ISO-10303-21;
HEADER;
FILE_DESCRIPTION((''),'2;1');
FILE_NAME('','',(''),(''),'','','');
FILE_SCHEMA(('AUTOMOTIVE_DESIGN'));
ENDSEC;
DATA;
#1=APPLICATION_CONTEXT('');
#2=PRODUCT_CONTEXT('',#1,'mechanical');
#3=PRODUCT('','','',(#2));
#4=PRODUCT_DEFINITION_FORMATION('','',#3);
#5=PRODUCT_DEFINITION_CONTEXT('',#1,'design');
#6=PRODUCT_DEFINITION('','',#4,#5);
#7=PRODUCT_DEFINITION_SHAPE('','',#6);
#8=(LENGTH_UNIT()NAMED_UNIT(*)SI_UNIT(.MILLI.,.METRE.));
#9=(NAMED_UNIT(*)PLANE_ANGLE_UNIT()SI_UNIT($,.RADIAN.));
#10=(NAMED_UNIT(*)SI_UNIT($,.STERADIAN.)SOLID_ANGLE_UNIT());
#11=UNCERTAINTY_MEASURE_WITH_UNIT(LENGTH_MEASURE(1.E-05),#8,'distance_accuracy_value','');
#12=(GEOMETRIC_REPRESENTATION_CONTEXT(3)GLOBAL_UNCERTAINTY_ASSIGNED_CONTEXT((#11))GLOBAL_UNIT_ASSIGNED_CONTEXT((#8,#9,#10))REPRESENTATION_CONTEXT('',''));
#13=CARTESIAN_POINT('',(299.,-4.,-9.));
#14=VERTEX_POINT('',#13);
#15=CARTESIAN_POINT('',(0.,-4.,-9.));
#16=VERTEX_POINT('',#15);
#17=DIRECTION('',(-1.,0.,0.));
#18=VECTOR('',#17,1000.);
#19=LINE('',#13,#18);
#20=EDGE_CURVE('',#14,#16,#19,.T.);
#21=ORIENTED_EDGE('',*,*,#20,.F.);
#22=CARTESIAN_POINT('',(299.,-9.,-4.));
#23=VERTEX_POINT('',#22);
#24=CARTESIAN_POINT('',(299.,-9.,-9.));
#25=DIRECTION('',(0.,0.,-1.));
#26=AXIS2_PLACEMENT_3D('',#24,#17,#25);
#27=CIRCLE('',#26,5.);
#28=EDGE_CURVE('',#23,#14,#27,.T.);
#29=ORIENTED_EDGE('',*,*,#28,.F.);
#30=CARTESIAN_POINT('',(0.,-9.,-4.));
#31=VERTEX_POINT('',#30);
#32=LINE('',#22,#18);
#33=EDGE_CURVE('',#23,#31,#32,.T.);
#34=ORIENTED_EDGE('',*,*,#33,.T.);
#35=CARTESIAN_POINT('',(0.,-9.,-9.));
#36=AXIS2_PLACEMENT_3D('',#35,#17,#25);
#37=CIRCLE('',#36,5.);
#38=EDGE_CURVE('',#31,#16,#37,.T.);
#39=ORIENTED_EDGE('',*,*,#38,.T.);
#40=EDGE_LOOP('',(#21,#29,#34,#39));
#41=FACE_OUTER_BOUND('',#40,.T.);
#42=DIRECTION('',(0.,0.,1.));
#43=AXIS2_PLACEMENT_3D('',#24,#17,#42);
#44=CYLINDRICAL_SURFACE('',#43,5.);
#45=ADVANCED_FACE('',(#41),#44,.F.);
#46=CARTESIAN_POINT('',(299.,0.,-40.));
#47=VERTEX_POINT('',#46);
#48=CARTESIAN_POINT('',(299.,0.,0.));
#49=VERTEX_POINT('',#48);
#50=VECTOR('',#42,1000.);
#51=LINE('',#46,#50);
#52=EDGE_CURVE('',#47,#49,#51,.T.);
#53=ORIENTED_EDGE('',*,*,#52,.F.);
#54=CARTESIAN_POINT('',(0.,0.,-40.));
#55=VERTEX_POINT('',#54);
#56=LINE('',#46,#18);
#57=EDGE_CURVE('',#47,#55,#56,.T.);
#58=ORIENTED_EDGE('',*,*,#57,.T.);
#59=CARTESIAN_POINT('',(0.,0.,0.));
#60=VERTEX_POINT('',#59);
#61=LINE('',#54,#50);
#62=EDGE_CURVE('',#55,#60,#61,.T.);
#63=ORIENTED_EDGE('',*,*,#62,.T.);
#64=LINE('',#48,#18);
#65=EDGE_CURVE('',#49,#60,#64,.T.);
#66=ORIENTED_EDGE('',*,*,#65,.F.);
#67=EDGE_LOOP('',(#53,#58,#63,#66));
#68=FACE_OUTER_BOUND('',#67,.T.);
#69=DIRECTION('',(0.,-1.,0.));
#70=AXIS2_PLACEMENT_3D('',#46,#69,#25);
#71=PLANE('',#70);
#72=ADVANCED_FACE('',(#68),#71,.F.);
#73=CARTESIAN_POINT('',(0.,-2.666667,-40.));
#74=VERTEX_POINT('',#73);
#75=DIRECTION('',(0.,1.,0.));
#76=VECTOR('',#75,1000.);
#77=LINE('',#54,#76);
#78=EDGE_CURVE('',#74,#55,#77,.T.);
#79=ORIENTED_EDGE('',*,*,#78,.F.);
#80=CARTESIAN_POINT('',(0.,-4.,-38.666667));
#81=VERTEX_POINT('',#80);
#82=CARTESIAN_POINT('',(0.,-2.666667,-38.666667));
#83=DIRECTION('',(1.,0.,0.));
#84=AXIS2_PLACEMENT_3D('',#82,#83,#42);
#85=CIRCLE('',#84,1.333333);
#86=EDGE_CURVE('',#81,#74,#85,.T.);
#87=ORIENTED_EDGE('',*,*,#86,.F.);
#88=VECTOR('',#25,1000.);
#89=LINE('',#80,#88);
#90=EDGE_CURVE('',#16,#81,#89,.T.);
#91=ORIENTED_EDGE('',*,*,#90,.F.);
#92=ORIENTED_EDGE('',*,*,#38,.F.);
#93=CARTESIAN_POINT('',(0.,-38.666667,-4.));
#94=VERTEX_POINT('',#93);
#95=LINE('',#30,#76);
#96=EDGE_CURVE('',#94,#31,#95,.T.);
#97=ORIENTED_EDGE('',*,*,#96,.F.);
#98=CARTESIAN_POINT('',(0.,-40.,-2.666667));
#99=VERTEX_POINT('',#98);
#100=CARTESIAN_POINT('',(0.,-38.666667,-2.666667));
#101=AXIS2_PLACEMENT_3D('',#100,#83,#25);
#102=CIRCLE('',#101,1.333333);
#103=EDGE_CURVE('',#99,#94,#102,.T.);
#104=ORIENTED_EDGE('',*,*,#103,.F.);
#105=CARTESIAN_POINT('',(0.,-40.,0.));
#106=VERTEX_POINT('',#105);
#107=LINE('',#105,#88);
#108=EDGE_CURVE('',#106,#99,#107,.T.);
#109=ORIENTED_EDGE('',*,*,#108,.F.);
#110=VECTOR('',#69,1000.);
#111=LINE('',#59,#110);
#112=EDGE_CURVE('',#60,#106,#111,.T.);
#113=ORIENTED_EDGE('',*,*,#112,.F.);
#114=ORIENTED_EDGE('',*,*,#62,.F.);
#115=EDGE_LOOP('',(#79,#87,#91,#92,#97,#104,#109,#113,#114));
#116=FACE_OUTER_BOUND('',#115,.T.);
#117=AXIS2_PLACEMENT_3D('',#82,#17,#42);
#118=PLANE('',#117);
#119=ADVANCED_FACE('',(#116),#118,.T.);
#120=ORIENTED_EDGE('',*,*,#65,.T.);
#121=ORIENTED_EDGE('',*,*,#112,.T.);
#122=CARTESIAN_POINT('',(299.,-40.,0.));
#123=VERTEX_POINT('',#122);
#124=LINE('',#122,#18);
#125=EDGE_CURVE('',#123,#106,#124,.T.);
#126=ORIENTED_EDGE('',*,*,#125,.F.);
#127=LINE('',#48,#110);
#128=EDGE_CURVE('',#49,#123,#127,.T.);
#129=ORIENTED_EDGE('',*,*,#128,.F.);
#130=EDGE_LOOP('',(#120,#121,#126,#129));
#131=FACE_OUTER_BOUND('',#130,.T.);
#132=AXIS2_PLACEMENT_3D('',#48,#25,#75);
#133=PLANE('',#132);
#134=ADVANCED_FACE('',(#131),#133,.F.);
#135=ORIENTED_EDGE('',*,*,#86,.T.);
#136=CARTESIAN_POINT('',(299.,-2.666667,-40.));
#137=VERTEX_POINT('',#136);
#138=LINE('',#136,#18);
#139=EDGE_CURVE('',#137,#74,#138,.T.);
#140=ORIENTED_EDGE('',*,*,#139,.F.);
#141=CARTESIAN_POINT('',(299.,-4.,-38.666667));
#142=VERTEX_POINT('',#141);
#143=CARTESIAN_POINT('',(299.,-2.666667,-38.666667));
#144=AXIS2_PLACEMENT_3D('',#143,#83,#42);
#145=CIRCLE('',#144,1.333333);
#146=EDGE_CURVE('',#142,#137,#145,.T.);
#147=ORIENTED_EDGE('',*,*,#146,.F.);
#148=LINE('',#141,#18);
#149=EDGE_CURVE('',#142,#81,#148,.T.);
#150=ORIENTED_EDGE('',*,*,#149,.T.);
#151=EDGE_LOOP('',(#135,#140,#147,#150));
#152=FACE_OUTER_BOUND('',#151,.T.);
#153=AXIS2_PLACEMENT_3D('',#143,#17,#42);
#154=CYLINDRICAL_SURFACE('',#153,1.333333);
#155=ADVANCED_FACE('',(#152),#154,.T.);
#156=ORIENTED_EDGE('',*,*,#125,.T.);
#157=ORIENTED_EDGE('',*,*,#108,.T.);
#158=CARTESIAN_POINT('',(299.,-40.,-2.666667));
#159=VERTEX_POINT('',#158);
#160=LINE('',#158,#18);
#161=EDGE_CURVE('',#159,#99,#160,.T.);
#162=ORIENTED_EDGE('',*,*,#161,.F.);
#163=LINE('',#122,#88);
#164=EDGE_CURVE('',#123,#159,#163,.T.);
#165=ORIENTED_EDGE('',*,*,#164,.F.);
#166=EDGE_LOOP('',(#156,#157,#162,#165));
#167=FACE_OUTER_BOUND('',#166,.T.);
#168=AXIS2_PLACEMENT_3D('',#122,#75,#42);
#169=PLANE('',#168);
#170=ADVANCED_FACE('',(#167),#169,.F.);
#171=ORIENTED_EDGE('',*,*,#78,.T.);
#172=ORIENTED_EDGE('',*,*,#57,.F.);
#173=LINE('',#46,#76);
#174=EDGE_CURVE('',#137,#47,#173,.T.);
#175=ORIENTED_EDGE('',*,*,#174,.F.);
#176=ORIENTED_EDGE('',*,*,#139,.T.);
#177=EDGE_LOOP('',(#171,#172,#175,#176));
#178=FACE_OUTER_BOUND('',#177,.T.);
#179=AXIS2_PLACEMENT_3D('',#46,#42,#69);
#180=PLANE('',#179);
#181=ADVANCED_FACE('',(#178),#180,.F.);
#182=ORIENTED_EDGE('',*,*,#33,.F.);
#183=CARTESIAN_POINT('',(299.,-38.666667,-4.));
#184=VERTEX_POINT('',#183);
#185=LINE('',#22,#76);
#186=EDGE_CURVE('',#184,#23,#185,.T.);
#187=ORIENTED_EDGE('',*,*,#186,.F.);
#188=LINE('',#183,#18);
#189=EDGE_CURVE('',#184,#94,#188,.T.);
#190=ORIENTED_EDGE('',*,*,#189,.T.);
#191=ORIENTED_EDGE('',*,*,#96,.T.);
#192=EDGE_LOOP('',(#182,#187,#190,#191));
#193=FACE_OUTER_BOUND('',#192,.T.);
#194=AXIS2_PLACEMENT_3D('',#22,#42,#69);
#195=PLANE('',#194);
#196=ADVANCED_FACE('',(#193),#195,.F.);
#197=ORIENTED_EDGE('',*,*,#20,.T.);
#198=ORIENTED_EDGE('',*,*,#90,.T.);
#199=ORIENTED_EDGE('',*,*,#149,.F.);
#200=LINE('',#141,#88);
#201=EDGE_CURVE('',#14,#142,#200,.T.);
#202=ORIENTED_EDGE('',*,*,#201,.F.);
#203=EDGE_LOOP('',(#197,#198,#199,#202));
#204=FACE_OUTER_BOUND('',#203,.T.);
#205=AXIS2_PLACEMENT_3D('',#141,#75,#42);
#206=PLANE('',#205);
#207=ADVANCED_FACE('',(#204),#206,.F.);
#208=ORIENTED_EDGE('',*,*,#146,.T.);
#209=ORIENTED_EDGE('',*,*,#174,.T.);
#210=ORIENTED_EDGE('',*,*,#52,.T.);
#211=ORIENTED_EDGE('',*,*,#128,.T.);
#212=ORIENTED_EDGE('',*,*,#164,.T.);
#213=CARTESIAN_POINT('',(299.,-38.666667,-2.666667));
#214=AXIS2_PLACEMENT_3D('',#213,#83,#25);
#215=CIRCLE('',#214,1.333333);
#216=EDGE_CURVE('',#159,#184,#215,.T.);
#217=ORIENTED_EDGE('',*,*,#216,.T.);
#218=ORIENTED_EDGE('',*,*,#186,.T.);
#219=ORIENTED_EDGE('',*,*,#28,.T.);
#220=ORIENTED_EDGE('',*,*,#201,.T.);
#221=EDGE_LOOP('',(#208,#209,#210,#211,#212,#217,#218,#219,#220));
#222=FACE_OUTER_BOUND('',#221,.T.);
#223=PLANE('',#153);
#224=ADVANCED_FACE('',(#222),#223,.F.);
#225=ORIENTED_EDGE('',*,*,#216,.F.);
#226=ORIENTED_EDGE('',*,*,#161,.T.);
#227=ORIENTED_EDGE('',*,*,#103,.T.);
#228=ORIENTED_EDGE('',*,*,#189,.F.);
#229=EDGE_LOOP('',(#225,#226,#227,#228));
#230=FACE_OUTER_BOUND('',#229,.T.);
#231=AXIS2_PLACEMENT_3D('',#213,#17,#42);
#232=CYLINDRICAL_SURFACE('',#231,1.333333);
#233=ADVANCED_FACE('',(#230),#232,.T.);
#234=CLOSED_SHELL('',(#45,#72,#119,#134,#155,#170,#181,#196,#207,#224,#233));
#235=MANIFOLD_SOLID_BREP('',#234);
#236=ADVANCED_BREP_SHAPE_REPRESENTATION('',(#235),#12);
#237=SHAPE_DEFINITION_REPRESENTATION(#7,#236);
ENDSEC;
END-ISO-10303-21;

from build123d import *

# Parameters (mm, degrees)
MEMBER_4X4_1_DEPTH = 299


with BuildPart() as part:
    # Sketch13 → Member 4X4_1 (new body)
    with BuildSketch(Plane(origin=(0, 0, 0), x_dir=(0, 0, -1), z_dir=(1, 0, 0))):
        with BuildLine():
            Line((40, 0), (0, 0))
            Line((0, 0), (0, -40))
            Line((0, -40), (2.666666667, -40))
            ThreePointArc((2.666666667, -40), (3.609475708, -39.609475708), (4, -38.666666667))
            Line((4, -38.666666667), (4, -9))
            ThreePointArc((4, -9), (5.464466094, -5.464466094), (9, -4))
            Line((9, -4), (38.666666667, -4))
            ThreePointArc((38.666666667, -4), (39.609475708, -3.609475708), (40, -2.666666667))
            Line((40, -2.666666667), (40, 0))
        make_face()
    extrude(amount=MEMBER_4X4_1_DEPTH)


solid = part.part
